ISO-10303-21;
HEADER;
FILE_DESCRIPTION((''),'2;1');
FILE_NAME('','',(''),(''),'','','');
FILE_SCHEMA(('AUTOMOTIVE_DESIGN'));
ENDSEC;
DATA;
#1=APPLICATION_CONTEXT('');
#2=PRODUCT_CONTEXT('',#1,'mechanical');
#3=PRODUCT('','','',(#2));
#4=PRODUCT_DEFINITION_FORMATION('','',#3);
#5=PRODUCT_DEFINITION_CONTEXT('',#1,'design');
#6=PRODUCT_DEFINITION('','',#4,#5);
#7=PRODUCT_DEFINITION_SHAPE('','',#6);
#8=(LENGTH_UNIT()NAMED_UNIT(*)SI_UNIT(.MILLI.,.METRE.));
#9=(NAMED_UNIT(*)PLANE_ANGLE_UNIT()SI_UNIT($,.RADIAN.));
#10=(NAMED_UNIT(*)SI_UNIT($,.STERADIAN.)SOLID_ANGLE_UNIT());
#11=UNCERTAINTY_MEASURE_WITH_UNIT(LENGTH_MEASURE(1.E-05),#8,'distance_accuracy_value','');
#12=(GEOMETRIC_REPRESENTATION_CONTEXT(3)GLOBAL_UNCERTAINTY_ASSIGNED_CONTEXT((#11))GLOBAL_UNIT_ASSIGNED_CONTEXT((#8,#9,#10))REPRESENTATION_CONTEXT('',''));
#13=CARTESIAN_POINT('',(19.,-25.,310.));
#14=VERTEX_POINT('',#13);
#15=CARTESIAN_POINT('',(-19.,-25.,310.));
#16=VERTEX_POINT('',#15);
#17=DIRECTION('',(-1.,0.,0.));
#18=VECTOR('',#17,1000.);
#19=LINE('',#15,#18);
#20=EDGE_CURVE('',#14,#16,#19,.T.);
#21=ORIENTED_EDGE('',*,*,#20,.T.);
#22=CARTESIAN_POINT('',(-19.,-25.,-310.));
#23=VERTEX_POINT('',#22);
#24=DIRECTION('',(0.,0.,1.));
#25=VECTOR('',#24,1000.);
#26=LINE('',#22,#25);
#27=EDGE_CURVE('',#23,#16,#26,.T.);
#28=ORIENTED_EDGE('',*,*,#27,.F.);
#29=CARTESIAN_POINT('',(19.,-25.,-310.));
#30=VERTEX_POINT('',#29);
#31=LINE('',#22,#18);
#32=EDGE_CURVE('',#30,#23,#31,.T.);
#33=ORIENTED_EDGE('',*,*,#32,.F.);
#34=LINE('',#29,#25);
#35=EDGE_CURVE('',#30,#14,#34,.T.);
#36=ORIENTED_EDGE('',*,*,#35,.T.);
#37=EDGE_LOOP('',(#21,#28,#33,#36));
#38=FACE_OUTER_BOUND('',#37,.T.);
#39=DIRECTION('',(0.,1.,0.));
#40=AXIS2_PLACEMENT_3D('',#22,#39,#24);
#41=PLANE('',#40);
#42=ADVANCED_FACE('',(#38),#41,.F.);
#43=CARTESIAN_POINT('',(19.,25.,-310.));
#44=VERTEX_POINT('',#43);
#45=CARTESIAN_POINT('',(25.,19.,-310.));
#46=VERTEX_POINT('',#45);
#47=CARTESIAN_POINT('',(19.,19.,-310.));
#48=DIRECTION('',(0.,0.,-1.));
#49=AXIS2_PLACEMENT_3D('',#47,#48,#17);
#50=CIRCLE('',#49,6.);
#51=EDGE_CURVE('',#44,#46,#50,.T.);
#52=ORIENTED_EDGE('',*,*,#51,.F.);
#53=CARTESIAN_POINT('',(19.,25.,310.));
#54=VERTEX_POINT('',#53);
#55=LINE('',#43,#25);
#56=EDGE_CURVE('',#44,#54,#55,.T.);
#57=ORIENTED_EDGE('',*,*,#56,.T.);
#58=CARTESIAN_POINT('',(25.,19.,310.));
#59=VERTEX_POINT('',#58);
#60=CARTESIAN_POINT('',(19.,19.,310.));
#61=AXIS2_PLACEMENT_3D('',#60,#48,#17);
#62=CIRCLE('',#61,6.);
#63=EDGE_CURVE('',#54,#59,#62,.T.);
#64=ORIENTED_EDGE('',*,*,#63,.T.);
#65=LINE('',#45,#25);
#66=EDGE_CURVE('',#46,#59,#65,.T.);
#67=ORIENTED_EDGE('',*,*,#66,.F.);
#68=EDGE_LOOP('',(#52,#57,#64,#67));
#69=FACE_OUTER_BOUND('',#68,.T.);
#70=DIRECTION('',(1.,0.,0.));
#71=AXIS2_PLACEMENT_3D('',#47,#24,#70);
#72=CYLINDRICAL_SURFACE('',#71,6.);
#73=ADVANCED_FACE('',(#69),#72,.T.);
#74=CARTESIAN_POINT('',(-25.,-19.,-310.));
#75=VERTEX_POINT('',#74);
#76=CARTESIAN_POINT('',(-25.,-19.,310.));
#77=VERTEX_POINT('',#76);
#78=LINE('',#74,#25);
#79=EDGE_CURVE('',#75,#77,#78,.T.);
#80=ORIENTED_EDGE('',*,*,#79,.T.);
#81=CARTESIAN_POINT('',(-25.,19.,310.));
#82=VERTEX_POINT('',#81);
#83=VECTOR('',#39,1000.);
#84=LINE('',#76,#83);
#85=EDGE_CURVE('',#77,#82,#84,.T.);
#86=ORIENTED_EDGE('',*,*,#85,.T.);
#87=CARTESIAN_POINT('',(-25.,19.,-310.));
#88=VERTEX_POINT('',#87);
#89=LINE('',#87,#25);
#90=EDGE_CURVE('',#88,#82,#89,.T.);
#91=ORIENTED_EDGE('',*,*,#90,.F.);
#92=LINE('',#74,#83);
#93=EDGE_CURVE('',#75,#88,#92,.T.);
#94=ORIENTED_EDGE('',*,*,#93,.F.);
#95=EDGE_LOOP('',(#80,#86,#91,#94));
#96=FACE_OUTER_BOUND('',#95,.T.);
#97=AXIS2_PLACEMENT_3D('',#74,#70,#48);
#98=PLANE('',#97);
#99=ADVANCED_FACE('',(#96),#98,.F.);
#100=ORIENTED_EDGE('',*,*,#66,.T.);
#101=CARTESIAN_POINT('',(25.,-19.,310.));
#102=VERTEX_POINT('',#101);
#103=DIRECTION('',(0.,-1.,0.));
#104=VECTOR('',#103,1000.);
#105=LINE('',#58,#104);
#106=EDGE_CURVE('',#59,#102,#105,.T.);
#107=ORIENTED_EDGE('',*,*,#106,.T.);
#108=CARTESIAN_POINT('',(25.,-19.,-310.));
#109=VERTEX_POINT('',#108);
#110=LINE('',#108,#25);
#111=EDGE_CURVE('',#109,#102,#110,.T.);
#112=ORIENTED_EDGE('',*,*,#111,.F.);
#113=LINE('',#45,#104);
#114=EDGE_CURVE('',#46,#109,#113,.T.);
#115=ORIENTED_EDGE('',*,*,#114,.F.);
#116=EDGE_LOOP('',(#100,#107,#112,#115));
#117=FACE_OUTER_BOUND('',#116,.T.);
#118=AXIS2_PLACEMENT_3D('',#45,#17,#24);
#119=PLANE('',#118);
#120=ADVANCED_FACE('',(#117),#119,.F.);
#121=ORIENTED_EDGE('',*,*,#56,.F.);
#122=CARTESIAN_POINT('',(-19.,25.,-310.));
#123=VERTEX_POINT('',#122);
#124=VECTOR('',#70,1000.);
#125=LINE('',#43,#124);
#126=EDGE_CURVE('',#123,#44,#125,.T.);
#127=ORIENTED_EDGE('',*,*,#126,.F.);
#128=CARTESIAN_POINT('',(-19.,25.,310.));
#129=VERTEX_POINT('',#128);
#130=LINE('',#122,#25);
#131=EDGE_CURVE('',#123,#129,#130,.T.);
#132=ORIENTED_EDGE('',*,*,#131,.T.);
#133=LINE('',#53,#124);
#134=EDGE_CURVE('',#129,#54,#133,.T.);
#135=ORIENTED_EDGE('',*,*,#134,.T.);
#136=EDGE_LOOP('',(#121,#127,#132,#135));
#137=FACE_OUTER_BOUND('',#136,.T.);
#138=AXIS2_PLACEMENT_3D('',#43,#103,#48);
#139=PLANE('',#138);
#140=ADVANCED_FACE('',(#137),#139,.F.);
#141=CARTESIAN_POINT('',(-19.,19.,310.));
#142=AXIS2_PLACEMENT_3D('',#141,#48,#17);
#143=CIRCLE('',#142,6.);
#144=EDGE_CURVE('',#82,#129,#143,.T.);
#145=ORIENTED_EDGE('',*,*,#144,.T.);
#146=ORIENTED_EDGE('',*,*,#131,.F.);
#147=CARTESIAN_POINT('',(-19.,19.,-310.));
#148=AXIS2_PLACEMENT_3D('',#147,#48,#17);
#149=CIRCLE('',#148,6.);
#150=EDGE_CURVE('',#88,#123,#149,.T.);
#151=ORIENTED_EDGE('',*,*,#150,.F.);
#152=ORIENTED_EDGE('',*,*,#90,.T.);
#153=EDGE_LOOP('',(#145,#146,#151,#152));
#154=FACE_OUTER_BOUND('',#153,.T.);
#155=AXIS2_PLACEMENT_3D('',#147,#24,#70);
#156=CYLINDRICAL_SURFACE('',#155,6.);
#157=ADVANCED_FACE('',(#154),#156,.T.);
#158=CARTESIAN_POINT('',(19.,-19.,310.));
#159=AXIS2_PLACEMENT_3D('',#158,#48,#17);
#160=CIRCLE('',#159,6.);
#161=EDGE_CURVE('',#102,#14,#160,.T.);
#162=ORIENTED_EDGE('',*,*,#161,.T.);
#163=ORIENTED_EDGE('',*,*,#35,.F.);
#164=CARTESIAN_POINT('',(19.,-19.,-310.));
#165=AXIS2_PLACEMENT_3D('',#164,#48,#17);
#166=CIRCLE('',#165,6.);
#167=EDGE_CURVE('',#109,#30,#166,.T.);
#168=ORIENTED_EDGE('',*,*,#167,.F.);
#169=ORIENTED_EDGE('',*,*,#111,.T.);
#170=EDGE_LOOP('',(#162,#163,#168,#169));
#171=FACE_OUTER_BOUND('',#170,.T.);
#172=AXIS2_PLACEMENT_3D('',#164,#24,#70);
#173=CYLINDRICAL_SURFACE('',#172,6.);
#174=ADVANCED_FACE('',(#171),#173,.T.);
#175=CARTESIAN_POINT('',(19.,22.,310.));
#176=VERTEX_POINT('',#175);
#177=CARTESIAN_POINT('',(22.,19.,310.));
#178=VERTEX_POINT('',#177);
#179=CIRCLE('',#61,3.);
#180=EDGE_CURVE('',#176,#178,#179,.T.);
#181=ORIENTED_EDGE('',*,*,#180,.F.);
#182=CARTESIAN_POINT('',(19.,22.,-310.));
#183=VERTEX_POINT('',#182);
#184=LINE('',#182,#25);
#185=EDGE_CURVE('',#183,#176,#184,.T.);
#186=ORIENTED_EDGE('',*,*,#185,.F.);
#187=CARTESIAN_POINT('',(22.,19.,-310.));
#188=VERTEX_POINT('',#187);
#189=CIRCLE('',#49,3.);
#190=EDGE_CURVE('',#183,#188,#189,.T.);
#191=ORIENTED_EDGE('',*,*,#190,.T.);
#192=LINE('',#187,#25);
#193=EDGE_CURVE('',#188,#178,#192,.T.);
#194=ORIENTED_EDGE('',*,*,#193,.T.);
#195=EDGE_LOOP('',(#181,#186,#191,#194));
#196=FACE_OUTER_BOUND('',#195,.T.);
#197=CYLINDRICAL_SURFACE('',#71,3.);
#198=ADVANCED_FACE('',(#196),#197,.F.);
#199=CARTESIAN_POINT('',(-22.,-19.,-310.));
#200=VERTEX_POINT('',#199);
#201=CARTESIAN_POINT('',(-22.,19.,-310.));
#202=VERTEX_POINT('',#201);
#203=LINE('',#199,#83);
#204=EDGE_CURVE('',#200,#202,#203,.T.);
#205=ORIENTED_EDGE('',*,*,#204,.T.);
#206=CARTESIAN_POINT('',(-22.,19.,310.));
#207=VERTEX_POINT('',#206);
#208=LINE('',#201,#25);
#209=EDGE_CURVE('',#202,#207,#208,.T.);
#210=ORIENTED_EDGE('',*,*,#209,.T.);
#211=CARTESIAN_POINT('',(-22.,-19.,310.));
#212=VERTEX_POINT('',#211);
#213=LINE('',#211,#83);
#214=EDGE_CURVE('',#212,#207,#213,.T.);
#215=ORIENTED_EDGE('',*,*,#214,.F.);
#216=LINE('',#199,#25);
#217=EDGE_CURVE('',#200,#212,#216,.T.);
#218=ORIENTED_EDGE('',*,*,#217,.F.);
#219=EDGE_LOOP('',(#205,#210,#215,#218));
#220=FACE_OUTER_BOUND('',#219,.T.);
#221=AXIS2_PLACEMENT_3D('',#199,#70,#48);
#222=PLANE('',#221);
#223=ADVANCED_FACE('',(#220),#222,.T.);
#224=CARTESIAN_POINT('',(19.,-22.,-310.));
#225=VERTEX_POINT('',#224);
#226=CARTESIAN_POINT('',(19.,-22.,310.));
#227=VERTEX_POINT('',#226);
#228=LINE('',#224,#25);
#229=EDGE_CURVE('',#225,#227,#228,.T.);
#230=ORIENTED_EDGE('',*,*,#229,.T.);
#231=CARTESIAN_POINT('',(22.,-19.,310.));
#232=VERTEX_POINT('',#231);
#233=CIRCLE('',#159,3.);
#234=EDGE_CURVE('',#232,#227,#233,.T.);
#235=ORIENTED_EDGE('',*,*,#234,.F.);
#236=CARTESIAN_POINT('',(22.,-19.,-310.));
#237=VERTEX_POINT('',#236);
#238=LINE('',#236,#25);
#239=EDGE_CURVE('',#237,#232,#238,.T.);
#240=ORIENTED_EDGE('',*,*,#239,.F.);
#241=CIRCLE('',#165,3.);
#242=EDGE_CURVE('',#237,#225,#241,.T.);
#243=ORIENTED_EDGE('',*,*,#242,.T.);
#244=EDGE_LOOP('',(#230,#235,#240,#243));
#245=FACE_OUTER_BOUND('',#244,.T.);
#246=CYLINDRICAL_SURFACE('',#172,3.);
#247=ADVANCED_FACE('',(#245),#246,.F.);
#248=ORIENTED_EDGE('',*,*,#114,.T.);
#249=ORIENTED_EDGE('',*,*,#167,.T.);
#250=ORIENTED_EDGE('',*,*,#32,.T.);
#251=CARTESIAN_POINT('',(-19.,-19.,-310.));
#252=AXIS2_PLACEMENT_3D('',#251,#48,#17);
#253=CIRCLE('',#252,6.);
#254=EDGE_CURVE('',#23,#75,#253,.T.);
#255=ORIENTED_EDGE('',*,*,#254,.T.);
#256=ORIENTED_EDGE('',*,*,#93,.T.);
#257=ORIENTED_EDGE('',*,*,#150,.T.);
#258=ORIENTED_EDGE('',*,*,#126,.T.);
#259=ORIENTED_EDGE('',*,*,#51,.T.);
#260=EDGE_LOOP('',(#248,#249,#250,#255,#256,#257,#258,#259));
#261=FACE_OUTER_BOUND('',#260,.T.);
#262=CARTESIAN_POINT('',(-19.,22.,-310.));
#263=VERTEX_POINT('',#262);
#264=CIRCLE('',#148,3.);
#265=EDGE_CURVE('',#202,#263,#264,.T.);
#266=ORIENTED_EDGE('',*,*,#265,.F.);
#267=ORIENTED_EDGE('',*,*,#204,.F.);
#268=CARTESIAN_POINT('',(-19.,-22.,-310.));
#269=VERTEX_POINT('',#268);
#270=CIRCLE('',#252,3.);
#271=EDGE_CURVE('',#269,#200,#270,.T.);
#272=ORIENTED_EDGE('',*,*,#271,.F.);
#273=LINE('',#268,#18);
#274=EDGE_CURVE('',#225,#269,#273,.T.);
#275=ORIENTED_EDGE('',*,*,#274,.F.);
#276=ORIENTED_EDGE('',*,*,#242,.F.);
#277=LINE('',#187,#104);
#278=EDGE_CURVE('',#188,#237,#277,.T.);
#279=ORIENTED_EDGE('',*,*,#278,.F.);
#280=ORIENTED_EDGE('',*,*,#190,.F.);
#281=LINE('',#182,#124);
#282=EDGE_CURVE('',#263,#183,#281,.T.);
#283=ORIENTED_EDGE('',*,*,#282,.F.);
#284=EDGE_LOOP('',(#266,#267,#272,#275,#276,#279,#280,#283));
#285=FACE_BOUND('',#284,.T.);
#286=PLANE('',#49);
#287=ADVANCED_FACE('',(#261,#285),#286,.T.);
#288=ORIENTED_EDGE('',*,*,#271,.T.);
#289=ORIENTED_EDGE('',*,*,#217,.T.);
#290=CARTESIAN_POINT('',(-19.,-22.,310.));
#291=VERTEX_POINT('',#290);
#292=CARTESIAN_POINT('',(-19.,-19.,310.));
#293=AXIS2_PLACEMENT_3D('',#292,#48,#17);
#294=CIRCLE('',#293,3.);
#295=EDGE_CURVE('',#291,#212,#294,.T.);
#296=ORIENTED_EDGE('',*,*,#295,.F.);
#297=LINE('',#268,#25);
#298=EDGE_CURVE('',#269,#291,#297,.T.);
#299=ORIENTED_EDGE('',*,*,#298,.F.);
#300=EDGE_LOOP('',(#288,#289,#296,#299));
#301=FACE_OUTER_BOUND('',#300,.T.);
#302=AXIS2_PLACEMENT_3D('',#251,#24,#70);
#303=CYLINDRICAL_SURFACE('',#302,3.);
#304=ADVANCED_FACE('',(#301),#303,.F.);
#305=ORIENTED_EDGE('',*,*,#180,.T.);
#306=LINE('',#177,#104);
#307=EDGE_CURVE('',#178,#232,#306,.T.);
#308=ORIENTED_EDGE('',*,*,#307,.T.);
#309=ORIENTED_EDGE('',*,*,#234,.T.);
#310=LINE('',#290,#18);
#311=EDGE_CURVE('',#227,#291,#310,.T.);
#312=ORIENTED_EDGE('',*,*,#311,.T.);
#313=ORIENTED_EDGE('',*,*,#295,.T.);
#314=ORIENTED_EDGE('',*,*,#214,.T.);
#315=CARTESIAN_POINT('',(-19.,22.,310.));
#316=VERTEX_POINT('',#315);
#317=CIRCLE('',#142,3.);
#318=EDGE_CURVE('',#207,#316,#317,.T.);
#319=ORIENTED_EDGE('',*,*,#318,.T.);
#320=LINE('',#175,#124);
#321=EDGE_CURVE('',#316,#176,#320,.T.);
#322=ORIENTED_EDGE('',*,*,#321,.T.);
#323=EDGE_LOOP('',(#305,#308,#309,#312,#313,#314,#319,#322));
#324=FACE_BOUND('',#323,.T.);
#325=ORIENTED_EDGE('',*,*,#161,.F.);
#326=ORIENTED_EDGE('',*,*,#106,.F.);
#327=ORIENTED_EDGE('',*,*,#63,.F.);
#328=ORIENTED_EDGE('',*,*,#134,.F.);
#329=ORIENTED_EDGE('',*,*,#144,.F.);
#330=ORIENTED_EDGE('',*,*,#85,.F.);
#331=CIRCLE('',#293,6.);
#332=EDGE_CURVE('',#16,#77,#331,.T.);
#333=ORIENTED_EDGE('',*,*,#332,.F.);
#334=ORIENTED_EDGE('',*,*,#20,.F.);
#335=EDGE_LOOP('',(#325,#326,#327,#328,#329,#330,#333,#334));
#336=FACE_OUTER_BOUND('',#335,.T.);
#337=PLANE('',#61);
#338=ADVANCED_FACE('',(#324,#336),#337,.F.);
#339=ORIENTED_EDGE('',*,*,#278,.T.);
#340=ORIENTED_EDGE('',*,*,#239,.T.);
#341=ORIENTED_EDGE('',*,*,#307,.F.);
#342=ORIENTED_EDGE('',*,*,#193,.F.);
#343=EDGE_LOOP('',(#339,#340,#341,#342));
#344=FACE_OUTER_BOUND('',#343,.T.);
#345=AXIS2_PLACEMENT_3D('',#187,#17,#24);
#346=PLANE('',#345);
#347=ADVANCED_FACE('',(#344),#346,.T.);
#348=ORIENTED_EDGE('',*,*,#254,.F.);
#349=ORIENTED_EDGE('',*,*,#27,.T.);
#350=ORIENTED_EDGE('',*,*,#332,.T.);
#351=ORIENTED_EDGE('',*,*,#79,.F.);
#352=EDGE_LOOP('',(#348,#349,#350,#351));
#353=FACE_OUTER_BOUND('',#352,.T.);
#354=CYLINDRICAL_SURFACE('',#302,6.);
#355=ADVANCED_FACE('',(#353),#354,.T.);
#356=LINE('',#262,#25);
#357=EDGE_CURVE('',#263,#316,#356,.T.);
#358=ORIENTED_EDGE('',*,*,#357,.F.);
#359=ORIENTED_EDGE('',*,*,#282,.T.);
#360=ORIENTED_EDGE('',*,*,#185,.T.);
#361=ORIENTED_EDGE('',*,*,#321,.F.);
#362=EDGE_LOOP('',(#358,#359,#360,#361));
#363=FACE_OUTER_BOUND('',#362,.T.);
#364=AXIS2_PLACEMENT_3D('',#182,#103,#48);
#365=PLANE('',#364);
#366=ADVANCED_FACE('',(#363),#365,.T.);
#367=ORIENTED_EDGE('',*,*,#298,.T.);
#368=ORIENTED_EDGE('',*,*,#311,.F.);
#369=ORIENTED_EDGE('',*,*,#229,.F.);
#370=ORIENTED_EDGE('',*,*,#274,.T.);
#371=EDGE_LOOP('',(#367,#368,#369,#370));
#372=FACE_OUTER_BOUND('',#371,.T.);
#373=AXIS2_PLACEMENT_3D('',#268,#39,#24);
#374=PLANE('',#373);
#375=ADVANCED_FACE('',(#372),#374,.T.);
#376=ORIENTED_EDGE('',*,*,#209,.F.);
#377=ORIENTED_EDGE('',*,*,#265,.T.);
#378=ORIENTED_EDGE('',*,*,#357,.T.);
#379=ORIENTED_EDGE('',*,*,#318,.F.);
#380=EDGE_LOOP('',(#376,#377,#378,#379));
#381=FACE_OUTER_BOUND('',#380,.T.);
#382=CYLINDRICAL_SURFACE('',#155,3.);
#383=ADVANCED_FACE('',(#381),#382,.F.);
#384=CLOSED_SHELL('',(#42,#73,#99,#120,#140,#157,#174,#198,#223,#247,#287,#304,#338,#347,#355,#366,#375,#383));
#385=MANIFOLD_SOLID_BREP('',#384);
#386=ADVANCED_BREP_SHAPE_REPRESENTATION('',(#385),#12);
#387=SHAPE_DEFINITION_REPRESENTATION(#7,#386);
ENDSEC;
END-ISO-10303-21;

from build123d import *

# Parameters (mm, degrees)
GB_6728_1986_050_X_50_X_3_1_DEPTH = 620


with BuildPart() as part:
    # Sketch1 → Gb／6728-1986方形空心型钢 050 X 50 X 3(1) (new body)
    with BuildSketch(Plane.YX.offset(-310)):
        with BuildLine():
            Line((-19, -25), (19, -25))
            ThreePointArc((19, -25), (23.242640687, -23.242640687), (25, -19))
            Line((25, -19), (25, 19))
            ThreePointArc((25, 19), (23.242640687, 23.242640687), (19, 25))
            Line((19, 25), (-19, 25))
            ThreePointArc((-19, 25), (-23.242640687, 23.242640687), (-25, 19))
            Line((-25, 19), (-25, -19))
            ThreePointArc((-25, -19), (-23.242640687, -23.242640687), (-19, -25))
        make_face()
        with BuildLine():
            Line((-19, -22), (19, -22))
            ThreePointArc((19, -22), (21.121320344, -21.121320344), (22, -19))
            Line((22, -19), (22, 19))
            ThreePointArc((22, 19), (21.121320344, 21.121320344), (19, 22))
            Line((19, 22), (-19, 22))
            ThreePointArc((-19, 22), (-21.121320344, 21.121320344), (-22, 19))
            Line((-22, 19), (-22, -19))
            ThreePointArc((-22, -19), (-21.121320344, -21.121320344), (-19, -22))
        make_face(mode=Mode.SUBTRACT)
    extrude(amount=GB_6728_1986_050_X_50_X_3_1_DEPTH)


solid = part.part
